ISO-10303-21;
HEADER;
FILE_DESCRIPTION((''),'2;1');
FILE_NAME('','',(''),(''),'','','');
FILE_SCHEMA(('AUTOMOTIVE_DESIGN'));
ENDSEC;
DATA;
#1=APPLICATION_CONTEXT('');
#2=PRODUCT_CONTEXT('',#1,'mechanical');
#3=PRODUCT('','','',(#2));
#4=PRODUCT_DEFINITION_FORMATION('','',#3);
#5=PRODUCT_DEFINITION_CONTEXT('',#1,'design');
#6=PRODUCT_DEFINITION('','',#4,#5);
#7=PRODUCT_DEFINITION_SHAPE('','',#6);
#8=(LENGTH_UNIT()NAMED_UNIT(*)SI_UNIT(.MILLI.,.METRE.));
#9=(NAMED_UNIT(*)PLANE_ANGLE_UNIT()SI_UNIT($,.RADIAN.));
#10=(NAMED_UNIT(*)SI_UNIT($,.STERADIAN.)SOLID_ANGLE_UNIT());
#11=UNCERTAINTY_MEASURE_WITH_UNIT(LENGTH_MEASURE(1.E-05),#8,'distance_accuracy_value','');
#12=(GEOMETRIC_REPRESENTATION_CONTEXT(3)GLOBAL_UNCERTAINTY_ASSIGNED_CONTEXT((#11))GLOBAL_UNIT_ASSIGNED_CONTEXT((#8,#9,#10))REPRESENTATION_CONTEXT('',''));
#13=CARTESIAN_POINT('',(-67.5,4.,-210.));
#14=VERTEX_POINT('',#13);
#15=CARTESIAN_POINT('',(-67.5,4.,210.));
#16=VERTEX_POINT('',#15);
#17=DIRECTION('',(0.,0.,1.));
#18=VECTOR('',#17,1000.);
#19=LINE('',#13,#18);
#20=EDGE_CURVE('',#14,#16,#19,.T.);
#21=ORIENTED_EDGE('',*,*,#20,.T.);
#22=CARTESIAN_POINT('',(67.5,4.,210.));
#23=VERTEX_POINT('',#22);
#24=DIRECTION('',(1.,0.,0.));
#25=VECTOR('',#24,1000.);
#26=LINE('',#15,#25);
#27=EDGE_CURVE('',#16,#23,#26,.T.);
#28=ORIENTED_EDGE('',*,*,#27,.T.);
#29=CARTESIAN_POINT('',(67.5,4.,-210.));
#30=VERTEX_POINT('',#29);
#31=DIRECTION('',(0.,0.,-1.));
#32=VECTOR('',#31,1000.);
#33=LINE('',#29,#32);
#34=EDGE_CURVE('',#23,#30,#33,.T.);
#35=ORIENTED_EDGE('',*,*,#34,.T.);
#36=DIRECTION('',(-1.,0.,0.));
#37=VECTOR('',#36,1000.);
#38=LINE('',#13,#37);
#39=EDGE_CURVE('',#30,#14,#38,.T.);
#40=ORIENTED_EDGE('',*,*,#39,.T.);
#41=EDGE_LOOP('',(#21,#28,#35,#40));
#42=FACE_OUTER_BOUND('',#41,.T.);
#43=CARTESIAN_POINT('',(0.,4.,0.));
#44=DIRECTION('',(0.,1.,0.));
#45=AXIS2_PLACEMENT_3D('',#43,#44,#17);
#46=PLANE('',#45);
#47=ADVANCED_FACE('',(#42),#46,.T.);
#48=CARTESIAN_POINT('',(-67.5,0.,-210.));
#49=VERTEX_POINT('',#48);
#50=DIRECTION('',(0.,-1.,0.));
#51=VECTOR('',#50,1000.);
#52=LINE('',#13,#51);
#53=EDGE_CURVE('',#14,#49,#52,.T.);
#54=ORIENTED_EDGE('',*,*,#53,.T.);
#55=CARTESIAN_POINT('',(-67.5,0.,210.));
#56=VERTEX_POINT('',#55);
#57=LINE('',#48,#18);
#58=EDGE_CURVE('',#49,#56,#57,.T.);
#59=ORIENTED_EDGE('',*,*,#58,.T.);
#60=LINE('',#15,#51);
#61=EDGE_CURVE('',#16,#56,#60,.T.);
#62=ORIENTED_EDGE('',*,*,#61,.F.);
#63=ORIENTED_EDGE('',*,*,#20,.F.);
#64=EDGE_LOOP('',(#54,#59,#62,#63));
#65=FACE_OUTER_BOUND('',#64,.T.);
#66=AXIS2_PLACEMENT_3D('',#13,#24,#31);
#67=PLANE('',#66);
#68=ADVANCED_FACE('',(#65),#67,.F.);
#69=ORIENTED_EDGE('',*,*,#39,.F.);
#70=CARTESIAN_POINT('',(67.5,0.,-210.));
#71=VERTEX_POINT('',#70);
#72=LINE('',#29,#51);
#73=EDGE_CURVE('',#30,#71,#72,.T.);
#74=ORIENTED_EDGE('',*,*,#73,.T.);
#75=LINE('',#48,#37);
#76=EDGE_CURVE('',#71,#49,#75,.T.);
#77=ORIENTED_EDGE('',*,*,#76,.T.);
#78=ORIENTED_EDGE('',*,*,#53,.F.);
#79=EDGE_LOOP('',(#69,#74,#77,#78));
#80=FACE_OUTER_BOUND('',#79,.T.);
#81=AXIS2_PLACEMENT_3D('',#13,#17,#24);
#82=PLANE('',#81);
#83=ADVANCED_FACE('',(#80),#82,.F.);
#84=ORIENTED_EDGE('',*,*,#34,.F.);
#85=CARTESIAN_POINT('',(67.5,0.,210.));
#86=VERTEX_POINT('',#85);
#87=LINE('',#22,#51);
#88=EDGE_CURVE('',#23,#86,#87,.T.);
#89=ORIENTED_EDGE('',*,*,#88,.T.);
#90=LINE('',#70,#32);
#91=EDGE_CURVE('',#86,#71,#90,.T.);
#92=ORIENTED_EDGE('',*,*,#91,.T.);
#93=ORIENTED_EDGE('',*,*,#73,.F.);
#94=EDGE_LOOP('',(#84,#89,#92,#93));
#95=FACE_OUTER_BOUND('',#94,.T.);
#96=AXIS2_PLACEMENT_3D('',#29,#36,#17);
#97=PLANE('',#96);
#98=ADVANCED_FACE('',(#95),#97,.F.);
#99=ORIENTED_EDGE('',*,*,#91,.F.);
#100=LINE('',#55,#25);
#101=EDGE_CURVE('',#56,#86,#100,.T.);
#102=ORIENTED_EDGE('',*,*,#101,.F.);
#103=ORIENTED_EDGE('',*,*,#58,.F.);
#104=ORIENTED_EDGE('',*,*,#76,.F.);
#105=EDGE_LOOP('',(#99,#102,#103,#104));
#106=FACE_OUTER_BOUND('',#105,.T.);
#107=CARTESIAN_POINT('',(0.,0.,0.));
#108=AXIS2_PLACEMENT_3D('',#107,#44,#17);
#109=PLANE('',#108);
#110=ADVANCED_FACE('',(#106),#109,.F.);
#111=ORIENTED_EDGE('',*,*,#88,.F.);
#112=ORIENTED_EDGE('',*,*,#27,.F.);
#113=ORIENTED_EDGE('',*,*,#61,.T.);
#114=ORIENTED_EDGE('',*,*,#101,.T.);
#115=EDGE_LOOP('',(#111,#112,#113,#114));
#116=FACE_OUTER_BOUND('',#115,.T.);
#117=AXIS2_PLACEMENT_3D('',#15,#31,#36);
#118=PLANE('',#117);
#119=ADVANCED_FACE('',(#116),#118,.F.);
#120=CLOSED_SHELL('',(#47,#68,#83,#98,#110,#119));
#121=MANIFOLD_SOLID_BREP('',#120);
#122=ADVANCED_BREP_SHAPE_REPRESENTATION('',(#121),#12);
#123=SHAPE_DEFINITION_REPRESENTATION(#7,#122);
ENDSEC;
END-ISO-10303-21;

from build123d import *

# Parameters (mm, degrees)
SKETCH1_W           = 135
SKETCH1_H           = 420
BOSS_EXTRUDE1_DEPTH = 4


with BuildPart() as part:
    # Sketch1 → Boss-Extrude1 (new body)
    with BuildSketch(Plane(origin=(0, 0, 0), x_dir=(1, 0, 0), z_dir=(0, 1, 0))):
        Rectangle(SKETCH1_W, SKETCH1_H)
    extrude(amount=BOSS_EXTRUDE1_DEPTH)


solid = part.part
